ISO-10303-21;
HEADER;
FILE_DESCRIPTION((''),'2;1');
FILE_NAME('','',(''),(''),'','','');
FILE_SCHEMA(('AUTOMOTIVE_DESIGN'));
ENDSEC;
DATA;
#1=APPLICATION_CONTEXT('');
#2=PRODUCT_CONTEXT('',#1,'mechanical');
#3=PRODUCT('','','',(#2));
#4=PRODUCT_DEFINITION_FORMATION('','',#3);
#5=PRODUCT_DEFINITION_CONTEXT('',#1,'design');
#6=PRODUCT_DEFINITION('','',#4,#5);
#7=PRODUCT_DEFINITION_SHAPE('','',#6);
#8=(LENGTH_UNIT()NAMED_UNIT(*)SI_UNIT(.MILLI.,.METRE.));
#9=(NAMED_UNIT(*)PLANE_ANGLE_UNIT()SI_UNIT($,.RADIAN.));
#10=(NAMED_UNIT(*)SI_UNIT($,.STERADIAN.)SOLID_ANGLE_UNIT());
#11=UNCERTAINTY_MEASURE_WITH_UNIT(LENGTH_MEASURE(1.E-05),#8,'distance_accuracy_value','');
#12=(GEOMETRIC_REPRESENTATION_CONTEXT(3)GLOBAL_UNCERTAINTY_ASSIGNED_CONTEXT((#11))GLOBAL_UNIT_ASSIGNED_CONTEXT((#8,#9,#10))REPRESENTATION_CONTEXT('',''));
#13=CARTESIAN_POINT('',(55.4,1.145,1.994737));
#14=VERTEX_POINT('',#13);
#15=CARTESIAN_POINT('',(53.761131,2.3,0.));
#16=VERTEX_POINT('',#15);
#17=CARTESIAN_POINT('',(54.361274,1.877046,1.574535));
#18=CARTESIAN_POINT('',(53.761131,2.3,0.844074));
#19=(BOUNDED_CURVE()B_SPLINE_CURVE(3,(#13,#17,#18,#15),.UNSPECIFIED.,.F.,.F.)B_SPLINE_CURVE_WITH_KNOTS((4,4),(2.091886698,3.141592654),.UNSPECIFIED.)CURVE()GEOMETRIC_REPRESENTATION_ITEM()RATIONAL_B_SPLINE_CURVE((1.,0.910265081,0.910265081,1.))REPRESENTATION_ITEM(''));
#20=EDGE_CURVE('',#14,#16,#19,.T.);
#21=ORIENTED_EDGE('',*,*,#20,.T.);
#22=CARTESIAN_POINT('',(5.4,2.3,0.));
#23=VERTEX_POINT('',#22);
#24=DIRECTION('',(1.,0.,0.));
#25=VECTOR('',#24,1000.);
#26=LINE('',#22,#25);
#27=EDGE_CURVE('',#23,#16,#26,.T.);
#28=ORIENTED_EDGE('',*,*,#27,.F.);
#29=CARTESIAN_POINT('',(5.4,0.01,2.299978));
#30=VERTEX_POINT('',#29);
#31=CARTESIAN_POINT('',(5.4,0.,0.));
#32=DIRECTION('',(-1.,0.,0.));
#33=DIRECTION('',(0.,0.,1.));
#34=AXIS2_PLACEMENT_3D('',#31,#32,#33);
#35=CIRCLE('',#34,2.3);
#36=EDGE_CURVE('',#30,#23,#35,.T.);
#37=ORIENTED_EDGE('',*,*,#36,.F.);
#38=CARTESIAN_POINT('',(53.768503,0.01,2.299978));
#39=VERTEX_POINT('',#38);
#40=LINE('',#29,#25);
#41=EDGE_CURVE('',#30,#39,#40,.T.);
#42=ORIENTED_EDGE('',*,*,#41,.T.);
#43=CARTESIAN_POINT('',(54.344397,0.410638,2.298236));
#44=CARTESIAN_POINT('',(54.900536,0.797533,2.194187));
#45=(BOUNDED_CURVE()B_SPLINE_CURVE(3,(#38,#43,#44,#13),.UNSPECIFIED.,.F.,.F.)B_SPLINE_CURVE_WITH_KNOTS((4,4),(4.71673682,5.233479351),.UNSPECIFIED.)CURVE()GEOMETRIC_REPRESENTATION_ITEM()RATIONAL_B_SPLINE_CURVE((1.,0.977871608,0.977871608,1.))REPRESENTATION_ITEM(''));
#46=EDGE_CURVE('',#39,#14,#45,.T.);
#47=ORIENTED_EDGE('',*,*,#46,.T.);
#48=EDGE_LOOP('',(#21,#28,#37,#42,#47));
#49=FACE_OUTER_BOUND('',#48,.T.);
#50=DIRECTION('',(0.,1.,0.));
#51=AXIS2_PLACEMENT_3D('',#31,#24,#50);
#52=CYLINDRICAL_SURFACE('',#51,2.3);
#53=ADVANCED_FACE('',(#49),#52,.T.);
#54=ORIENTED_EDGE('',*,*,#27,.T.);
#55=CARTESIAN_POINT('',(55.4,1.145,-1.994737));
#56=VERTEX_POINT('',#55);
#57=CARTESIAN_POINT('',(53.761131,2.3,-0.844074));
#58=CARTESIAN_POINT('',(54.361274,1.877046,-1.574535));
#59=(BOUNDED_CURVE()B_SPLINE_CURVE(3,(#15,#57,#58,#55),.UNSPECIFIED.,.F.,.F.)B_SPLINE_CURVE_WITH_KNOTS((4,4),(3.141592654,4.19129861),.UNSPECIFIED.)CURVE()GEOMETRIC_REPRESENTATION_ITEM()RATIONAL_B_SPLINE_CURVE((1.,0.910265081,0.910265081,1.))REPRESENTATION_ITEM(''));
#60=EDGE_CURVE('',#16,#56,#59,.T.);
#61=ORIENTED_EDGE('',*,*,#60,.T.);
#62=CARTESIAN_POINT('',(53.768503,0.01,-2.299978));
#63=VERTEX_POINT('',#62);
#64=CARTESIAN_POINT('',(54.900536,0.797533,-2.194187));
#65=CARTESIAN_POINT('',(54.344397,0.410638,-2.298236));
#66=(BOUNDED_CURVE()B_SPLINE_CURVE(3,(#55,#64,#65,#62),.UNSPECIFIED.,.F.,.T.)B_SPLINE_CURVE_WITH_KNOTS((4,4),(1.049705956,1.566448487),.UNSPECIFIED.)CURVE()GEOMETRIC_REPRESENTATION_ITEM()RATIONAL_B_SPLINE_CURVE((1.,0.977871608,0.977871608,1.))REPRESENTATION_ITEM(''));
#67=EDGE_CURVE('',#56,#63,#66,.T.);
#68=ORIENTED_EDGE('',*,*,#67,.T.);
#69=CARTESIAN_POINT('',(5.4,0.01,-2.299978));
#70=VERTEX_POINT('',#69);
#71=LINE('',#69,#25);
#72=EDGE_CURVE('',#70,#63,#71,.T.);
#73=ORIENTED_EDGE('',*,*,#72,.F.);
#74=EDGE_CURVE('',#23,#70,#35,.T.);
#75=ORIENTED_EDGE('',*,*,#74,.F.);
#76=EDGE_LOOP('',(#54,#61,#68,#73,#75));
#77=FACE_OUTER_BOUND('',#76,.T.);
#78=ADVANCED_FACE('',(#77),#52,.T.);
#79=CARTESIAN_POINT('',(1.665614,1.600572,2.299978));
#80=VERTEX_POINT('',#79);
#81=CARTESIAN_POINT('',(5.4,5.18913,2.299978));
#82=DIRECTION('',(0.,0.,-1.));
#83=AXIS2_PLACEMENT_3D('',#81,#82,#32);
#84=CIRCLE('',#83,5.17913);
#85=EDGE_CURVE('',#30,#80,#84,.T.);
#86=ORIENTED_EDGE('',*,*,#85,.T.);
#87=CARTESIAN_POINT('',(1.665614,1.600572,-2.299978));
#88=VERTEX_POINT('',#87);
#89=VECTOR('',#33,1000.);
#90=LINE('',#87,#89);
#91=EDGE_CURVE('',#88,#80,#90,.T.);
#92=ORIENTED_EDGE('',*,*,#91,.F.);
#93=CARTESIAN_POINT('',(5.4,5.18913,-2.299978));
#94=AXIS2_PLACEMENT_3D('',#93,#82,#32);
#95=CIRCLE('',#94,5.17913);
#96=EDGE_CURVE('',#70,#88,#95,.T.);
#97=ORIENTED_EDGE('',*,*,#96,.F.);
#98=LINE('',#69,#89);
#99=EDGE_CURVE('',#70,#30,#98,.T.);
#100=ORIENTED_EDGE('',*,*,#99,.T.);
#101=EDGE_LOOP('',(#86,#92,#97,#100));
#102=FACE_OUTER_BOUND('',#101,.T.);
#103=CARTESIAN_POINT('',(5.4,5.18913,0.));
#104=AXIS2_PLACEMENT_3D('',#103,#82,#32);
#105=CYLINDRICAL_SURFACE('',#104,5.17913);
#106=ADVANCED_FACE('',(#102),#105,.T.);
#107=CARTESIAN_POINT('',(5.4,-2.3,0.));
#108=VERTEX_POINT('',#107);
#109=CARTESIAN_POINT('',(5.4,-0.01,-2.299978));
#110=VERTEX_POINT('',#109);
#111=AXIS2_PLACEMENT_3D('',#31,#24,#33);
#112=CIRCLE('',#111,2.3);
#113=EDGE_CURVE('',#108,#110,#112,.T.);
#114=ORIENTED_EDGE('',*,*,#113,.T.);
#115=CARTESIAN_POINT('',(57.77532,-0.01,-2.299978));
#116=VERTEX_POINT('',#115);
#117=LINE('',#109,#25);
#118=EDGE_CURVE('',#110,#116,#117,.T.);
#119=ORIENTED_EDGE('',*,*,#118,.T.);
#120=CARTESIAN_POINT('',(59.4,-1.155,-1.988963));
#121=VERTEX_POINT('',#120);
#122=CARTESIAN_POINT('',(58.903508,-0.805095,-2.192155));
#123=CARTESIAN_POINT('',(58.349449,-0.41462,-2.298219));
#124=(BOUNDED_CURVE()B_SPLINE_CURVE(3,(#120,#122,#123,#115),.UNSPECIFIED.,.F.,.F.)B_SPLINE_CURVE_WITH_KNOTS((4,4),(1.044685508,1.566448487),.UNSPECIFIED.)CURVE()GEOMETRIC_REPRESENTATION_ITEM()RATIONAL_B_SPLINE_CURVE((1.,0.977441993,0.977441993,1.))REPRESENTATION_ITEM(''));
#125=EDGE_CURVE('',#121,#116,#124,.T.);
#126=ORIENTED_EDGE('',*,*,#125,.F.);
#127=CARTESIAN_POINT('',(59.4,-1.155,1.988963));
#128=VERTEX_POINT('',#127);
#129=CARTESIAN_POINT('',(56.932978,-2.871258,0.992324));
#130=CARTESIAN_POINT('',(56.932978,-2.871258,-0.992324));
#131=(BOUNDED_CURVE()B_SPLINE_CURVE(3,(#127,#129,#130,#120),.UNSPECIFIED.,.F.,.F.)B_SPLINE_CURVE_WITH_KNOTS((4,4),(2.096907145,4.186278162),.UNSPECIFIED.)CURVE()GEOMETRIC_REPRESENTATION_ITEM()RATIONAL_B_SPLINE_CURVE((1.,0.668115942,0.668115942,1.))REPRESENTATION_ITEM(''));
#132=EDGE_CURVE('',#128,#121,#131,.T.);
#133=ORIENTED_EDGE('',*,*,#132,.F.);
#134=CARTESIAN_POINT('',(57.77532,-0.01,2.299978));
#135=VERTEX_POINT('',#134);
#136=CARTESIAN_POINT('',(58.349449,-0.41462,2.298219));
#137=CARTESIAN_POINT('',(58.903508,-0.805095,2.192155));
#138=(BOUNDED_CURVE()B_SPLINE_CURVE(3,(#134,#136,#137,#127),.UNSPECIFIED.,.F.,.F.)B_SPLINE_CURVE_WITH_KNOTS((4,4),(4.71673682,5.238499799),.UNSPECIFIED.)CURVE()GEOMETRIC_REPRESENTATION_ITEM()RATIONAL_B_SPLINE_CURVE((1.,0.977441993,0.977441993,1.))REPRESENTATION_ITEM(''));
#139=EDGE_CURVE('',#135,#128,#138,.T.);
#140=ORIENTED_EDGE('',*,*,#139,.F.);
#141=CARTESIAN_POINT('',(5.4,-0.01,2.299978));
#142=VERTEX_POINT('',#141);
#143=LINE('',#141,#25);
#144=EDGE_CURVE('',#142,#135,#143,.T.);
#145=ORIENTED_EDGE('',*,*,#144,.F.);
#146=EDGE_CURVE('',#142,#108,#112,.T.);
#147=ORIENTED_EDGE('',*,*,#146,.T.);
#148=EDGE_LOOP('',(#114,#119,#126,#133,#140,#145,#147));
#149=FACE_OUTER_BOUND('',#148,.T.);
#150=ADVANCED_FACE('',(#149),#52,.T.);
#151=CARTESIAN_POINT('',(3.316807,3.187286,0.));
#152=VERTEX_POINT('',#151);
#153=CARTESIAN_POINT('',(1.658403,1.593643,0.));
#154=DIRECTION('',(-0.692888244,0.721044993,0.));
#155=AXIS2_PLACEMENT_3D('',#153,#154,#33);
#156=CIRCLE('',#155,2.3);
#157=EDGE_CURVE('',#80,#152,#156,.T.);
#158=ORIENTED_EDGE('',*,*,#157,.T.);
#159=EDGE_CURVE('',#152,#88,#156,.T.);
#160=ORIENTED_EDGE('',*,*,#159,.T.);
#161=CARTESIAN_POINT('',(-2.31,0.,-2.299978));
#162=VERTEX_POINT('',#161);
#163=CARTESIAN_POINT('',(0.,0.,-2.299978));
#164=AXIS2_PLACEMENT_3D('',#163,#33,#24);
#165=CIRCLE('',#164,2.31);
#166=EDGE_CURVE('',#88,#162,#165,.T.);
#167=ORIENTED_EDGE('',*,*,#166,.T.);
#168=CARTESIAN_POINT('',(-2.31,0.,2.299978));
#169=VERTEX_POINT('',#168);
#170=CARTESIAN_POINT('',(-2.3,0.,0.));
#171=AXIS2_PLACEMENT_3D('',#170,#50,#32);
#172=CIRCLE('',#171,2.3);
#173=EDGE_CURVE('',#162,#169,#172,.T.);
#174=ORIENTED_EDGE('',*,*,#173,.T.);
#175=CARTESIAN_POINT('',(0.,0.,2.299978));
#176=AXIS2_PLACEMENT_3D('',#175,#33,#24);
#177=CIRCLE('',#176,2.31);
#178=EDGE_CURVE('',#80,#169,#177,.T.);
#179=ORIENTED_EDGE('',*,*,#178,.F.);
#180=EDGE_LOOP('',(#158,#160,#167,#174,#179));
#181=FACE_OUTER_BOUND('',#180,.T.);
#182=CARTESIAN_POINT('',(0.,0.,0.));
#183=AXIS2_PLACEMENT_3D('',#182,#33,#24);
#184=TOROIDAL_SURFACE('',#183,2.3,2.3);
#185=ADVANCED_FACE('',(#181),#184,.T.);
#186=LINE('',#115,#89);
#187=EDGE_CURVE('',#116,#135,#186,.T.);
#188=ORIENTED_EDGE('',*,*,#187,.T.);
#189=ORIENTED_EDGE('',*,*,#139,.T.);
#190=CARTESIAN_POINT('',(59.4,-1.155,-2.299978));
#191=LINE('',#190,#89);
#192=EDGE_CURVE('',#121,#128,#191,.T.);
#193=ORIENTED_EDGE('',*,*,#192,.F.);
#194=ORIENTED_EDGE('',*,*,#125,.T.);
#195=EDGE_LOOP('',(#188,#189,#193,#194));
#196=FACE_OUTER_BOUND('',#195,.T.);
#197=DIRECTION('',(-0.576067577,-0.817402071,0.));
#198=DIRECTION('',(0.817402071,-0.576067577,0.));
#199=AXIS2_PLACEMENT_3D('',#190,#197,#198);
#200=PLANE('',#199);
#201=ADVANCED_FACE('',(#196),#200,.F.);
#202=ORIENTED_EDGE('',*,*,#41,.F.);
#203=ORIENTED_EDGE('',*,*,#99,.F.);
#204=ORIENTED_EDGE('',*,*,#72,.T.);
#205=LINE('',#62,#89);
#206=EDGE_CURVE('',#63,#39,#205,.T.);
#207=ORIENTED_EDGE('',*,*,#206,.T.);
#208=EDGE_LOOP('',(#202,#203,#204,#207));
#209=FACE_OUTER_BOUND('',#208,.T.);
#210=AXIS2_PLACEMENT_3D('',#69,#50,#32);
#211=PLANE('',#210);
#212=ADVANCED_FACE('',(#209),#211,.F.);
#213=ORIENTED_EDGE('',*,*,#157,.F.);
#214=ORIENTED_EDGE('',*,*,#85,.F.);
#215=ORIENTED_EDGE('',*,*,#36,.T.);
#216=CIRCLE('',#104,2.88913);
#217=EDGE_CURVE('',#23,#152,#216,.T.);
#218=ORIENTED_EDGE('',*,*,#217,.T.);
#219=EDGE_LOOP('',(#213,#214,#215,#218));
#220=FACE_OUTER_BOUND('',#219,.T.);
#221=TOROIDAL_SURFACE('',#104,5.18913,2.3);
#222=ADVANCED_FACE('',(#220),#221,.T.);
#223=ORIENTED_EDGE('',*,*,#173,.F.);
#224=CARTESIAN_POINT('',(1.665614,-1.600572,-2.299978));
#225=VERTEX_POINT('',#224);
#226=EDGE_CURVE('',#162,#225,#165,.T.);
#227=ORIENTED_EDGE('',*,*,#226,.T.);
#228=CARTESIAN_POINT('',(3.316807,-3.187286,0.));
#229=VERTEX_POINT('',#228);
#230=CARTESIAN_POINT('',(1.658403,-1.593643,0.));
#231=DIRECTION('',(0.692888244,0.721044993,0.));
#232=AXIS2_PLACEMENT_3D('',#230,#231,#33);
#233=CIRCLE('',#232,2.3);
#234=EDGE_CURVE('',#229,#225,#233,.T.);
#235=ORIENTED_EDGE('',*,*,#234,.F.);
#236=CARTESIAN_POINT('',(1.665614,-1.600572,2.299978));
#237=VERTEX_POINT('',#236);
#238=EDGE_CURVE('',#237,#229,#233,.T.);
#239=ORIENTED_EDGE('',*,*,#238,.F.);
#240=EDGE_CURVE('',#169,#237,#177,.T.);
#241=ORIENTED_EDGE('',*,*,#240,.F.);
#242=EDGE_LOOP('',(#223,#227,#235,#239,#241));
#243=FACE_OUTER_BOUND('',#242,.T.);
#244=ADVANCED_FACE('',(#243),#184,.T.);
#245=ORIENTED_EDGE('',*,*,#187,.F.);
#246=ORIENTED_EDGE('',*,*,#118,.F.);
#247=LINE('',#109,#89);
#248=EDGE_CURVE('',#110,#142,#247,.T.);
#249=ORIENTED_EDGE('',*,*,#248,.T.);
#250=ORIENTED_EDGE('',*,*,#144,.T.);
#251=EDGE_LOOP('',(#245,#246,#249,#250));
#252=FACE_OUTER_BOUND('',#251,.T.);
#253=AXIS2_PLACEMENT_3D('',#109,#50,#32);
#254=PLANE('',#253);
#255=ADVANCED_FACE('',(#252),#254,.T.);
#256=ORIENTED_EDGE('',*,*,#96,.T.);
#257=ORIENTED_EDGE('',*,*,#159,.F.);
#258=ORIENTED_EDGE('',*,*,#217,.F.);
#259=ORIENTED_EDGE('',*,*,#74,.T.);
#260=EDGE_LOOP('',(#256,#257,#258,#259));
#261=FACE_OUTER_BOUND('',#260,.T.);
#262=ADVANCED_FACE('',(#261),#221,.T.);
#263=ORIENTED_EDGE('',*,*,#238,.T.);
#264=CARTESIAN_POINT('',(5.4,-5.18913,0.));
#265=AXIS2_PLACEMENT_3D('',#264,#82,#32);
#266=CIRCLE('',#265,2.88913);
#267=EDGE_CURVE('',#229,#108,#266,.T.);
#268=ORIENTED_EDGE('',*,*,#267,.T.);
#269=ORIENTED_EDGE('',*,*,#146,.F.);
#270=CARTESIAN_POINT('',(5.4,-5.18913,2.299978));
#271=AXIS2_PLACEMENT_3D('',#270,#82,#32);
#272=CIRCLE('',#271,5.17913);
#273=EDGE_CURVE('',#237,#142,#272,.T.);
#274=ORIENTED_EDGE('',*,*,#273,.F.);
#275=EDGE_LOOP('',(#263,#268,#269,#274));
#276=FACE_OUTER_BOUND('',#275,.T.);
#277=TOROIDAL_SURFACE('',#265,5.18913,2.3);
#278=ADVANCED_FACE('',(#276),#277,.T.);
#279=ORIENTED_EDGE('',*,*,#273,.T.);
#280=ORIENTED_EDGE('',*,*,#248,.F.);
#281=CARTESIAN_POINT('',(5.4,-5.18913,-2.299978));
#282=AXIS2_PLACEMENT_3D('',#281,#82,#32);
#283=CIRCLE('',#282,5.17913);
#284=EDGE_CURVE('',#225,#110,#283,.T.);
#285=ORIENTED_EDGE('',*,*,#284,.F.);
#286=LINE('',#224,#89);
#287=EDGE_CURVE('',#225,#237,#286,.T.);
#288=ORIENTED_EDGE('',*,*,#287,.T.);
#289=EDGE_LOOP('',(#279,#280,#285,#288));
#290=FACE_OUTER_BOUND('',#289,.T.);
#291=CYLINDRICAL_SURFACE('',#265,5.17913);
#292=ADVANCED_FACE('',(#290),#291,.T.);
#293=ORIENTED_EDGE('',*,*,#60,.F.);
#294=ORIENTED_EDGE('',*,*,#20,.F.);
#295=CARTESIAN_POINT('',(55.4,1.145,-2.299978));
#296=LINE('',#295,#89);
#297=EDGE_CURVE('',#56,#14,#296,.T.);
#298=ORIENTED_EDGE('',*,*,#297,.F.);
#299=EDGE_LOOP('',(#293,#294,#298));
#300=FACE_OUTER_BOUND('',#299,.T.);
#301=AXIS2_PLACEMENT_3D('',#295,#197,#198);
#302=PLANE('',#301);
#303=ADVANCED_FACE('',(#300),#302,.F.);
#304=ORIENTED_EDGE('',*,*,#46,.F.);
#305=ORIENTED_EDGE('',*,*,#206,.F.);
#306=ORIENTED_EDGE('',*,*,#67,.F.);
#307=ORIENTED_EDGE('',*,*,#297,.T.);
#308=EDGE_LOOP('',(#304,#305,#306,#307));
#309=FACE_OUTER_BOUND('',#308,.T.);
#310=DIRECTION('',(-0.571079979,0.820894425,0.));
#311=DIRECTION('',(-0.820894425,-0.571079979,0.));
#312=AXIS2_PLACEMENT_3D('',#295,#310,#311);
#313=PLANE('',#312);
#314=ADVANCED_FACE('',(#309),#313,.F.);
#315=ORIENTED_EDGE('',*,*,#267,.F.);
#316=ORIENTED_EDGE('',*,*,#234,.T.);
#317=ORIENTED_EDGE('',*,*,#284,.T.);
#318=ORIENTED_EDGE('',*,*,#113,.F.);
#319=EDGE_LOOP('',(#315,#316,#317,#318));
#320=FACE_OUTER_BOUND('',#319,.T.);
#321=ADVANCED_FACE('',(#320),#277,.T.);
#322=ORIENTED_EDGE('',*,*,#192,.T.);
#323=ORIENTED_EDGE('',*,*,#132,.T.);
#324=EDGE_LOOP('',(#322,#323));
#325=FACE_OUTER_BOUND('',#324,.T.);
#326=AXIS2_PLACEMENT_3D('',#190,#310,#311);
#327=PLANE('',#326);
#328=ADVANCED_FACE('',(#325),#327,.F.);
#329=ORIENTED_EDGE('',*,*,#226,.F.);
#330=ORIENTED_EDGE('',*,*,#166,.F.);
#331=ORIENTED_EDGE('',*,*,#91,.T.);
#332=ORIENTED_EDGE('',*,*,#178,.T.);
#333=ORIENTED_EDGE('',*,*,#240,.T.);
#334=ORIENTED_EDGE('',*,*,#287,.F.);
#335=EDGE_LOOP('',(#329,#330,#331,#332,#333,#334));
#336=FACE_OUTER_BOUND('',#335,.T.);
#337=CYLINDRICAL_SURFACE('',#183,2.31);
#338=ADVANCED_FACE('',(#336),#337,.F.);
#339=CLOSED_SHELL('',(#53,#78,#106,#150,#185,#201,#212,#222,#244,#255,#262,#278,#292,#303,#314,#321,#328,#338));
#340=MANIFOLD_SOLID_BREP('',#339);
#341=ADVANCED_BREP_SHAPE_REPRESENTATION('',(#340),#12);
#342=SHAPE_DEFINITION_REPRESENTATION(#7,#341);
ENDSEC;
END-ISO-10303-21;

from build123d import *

# Parameters (mm, degrees)
CUT_EXTRUDE_1_DEPTH      = 60.622226572
CUT_EXTRUDE_1_DEPTH_BACK = 60.622226572


with BuildPart() as part:
    # 扫描2: sweep along a path in Sketch 203
    with BuildLine(Plane.XY) as sweep_2_path:
        Line((55.4, 2.3), (5.4, 2.3))
        ThreePointArc((5.4, 2.3), (4.267859381, 2.531061156), (3.316806967, 3.187285922))
        ThreePointArc((3.316806967, 3.187285922), (-4.6, 0), (3.316806967, -3.187285922))
        ThreePointArc((3.316806967, -3.187285922), (4.267859381, -2.531061156), (5.4, -2.3))
        Line((5.4, -2.3), (59.4, -2.3))
    # 草图2 → 扫描2 (sweep)
    with BuildSketch(Plane(origin=(55.4, 2.3, 0), x_dir=(0, 0, 1), z_dir=(-1, 0, 0))):
        with BuildLine():
            Line((-2.299978261, -2.29), (2.299978261, -2.29))
            ThreePointArc((2.299978261, -2.29), (0, 0), (-2.299978261, -2.29))
        make_face()
    sweep(path=sweep_2_path.line)

    # 草图3 → 切除-拉伸1 (cut, two sides: drawn at the far end of the back side and taken through both)
    with BuildSketch(Plane.XY.offset(-CUT_EXTRUDE_1_DEPTH_BACK)):
        Polygon((55.4, 1.145), (53.76113083, 2.3), (59.41, 2.3), (59.41, -2.3), (57.754128755, -2.3), (59.4, -1.155), (57.76113083, 0), (53.754128755, 0), align=None)
    extrude(amount=CUT_EXTRUDE_1_DEPTH + CUT_EXTRUDE_1_DEPTH_BACK, mode=Mode.SUBTRACT)


solid = part.part
